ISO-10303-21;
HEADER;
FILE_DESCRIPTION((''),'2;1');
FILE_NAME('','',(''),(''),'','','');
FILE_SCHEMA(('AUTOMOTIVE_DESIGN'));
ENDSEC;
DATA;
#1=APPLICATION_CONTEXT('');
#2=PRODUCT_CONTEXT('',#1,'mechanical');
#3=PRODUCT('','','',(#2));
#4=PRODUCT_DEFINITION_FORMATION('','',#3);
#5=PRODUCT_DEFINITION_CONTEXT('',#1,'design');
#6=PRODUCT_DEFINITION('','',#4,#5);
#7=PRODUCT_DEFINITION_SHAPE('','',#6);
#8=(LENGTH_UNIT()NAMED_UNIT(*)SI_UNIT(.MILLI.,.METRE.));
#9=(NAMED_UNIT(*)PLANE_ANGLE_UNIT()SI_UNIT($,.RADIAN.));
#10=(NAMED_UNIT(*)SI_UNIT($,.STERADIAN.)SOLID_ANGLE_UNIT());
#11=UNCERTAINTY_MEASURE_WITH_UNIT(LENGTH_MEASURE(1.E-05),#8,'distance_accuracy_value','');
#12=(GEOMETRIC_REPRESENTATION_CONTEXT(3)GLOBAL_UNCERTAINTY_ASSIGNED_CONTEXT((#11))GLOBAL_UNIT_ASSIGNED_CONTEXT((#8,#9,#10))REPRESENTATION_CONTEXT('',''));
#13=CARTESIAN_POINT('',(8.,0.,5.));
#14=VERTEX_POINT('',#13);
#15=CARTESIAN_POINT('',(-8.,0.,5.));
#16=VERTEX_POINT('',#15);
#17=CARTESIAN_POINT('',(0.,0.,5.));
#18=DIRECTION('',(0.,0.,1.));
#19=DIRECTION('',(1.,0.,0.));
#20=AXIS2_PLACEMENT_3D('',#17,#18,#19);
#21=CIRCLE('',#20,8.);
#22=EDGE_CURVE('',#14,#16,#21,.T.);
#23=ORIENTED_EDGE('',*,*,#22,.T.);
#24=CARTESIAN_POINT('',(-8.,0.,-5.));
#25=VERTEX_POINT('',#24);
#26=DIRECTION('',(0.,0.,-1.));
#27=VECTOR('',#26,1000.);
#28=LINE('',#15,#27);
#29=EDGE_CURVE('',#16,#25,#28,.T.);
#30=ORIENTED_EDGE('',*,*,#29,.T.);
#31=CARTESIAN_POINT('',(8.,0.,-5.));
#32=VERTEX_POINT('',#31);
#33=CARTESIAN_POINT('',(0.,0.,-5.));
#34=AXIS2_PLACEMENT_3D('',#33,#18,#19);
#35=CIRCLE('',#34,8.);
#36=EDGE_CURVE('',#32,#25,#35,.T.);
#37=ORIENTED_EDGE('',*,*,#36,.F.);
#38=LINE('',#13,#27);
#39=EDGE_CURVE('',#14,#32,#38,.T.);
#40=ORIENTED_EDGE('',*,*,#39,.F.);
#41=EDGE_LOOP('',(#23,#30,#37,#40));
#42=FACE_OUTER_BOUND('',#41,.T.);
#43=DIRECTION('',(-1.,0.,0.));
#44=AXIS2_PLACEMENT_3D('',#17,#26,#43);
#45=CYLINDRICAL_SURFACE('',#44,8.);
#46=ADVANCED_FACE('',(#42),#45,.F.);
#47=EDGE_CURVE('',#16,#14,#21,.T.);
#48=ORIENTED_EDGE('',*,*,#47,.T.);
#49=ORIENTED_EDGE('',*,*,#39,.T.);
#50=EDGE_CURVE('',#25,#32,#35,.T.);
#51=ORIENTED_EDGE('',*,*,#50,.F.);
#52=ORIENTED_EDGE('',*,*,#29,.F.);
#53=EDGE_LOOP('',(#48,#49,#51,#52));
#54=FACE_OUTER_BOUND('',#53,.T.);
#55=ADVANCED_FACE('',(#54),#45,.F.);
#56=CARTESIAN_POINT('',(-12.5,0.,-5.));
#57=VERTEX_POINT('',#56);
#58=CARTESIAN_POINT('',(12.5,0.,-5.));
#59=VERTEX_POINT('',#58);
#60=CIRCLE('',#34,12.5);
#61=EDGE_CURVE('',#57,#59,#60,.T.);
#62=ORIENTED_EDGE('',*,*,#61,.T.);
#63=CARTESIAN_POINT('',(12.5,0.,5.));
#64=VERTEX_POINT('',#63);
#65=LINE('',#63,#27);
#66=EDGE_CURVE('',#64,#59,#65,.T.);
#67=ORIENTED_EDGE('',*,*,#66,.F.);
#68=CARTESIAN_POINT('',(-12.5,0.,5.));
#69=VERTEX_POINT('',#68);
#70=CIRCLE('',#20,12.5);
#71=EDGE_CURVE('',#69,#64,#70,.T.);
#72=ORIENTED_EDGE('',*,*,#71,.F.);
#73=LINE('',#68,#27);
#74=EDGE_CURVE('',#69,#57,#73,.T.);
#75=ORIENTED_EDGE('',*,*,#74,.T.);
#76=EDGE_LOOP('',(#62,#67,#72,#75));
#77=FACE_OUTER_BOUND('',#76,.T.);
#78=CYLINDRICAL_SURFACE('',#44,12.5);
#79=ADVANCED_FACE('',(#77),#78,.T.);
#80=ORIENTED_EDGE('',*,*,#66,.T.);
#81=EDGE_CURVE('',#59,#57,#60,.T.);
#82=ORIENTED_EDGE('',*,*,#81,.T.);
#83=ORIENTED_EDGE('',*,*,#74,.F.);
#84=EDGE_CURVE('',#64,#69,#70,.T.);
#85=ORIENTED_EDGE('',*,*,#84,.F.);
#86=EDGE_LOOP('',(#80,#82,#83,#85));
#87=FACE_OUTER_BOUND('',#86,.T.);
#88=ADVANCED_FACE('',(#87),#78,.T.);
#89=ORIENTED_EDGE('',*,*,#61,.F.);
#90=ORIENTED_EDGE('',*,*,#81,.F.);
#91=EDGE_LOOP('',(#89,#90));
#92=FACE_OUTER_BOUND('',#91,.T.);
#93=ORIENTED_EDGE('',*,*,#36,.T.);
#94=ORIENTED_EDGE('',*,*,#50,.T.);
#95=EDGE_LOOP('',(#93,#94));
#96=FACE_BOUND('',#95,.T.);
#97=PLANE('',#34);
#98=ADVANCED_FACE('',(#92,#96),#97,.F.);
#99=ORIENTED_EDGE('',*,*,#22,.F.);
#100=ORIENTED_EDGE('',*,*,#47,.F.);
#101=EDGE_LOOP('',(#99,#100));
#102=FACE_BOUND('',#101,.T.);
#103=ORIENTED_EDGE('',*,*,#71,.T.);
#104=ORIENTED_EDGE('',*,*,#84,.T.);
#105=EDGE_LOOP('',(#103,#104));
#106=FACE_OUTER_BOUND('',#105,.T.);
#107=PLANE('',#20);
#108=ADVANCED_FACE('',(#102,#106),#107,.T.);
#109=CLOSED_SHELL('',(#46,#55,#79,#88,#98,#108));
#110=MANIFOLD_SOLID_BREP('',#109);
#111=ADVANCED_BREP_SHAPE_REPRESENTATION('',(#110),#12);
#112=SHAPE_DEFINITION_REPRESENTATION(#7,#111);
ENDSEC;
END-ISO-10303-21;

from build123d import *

# Parameters (mm, degrees)
SKETCH_1_R      = 12.5
SKETCH_1_R_2    = 8
EXTRUDE_1_DEPTH = 5


with BuildPart() as part:
    # 草图1 → 凸台-拉伸1 (new, symmetric)
    with BuildSketch(Plane.XY):
        Circle(SKETCH_1_R)
        Circle(SKETCH_1_R_2, mode=Mode.SUBTRACT)
    extrude(amount=EXTRUDE_1_DEPTH, both=True)


solid = part.part
